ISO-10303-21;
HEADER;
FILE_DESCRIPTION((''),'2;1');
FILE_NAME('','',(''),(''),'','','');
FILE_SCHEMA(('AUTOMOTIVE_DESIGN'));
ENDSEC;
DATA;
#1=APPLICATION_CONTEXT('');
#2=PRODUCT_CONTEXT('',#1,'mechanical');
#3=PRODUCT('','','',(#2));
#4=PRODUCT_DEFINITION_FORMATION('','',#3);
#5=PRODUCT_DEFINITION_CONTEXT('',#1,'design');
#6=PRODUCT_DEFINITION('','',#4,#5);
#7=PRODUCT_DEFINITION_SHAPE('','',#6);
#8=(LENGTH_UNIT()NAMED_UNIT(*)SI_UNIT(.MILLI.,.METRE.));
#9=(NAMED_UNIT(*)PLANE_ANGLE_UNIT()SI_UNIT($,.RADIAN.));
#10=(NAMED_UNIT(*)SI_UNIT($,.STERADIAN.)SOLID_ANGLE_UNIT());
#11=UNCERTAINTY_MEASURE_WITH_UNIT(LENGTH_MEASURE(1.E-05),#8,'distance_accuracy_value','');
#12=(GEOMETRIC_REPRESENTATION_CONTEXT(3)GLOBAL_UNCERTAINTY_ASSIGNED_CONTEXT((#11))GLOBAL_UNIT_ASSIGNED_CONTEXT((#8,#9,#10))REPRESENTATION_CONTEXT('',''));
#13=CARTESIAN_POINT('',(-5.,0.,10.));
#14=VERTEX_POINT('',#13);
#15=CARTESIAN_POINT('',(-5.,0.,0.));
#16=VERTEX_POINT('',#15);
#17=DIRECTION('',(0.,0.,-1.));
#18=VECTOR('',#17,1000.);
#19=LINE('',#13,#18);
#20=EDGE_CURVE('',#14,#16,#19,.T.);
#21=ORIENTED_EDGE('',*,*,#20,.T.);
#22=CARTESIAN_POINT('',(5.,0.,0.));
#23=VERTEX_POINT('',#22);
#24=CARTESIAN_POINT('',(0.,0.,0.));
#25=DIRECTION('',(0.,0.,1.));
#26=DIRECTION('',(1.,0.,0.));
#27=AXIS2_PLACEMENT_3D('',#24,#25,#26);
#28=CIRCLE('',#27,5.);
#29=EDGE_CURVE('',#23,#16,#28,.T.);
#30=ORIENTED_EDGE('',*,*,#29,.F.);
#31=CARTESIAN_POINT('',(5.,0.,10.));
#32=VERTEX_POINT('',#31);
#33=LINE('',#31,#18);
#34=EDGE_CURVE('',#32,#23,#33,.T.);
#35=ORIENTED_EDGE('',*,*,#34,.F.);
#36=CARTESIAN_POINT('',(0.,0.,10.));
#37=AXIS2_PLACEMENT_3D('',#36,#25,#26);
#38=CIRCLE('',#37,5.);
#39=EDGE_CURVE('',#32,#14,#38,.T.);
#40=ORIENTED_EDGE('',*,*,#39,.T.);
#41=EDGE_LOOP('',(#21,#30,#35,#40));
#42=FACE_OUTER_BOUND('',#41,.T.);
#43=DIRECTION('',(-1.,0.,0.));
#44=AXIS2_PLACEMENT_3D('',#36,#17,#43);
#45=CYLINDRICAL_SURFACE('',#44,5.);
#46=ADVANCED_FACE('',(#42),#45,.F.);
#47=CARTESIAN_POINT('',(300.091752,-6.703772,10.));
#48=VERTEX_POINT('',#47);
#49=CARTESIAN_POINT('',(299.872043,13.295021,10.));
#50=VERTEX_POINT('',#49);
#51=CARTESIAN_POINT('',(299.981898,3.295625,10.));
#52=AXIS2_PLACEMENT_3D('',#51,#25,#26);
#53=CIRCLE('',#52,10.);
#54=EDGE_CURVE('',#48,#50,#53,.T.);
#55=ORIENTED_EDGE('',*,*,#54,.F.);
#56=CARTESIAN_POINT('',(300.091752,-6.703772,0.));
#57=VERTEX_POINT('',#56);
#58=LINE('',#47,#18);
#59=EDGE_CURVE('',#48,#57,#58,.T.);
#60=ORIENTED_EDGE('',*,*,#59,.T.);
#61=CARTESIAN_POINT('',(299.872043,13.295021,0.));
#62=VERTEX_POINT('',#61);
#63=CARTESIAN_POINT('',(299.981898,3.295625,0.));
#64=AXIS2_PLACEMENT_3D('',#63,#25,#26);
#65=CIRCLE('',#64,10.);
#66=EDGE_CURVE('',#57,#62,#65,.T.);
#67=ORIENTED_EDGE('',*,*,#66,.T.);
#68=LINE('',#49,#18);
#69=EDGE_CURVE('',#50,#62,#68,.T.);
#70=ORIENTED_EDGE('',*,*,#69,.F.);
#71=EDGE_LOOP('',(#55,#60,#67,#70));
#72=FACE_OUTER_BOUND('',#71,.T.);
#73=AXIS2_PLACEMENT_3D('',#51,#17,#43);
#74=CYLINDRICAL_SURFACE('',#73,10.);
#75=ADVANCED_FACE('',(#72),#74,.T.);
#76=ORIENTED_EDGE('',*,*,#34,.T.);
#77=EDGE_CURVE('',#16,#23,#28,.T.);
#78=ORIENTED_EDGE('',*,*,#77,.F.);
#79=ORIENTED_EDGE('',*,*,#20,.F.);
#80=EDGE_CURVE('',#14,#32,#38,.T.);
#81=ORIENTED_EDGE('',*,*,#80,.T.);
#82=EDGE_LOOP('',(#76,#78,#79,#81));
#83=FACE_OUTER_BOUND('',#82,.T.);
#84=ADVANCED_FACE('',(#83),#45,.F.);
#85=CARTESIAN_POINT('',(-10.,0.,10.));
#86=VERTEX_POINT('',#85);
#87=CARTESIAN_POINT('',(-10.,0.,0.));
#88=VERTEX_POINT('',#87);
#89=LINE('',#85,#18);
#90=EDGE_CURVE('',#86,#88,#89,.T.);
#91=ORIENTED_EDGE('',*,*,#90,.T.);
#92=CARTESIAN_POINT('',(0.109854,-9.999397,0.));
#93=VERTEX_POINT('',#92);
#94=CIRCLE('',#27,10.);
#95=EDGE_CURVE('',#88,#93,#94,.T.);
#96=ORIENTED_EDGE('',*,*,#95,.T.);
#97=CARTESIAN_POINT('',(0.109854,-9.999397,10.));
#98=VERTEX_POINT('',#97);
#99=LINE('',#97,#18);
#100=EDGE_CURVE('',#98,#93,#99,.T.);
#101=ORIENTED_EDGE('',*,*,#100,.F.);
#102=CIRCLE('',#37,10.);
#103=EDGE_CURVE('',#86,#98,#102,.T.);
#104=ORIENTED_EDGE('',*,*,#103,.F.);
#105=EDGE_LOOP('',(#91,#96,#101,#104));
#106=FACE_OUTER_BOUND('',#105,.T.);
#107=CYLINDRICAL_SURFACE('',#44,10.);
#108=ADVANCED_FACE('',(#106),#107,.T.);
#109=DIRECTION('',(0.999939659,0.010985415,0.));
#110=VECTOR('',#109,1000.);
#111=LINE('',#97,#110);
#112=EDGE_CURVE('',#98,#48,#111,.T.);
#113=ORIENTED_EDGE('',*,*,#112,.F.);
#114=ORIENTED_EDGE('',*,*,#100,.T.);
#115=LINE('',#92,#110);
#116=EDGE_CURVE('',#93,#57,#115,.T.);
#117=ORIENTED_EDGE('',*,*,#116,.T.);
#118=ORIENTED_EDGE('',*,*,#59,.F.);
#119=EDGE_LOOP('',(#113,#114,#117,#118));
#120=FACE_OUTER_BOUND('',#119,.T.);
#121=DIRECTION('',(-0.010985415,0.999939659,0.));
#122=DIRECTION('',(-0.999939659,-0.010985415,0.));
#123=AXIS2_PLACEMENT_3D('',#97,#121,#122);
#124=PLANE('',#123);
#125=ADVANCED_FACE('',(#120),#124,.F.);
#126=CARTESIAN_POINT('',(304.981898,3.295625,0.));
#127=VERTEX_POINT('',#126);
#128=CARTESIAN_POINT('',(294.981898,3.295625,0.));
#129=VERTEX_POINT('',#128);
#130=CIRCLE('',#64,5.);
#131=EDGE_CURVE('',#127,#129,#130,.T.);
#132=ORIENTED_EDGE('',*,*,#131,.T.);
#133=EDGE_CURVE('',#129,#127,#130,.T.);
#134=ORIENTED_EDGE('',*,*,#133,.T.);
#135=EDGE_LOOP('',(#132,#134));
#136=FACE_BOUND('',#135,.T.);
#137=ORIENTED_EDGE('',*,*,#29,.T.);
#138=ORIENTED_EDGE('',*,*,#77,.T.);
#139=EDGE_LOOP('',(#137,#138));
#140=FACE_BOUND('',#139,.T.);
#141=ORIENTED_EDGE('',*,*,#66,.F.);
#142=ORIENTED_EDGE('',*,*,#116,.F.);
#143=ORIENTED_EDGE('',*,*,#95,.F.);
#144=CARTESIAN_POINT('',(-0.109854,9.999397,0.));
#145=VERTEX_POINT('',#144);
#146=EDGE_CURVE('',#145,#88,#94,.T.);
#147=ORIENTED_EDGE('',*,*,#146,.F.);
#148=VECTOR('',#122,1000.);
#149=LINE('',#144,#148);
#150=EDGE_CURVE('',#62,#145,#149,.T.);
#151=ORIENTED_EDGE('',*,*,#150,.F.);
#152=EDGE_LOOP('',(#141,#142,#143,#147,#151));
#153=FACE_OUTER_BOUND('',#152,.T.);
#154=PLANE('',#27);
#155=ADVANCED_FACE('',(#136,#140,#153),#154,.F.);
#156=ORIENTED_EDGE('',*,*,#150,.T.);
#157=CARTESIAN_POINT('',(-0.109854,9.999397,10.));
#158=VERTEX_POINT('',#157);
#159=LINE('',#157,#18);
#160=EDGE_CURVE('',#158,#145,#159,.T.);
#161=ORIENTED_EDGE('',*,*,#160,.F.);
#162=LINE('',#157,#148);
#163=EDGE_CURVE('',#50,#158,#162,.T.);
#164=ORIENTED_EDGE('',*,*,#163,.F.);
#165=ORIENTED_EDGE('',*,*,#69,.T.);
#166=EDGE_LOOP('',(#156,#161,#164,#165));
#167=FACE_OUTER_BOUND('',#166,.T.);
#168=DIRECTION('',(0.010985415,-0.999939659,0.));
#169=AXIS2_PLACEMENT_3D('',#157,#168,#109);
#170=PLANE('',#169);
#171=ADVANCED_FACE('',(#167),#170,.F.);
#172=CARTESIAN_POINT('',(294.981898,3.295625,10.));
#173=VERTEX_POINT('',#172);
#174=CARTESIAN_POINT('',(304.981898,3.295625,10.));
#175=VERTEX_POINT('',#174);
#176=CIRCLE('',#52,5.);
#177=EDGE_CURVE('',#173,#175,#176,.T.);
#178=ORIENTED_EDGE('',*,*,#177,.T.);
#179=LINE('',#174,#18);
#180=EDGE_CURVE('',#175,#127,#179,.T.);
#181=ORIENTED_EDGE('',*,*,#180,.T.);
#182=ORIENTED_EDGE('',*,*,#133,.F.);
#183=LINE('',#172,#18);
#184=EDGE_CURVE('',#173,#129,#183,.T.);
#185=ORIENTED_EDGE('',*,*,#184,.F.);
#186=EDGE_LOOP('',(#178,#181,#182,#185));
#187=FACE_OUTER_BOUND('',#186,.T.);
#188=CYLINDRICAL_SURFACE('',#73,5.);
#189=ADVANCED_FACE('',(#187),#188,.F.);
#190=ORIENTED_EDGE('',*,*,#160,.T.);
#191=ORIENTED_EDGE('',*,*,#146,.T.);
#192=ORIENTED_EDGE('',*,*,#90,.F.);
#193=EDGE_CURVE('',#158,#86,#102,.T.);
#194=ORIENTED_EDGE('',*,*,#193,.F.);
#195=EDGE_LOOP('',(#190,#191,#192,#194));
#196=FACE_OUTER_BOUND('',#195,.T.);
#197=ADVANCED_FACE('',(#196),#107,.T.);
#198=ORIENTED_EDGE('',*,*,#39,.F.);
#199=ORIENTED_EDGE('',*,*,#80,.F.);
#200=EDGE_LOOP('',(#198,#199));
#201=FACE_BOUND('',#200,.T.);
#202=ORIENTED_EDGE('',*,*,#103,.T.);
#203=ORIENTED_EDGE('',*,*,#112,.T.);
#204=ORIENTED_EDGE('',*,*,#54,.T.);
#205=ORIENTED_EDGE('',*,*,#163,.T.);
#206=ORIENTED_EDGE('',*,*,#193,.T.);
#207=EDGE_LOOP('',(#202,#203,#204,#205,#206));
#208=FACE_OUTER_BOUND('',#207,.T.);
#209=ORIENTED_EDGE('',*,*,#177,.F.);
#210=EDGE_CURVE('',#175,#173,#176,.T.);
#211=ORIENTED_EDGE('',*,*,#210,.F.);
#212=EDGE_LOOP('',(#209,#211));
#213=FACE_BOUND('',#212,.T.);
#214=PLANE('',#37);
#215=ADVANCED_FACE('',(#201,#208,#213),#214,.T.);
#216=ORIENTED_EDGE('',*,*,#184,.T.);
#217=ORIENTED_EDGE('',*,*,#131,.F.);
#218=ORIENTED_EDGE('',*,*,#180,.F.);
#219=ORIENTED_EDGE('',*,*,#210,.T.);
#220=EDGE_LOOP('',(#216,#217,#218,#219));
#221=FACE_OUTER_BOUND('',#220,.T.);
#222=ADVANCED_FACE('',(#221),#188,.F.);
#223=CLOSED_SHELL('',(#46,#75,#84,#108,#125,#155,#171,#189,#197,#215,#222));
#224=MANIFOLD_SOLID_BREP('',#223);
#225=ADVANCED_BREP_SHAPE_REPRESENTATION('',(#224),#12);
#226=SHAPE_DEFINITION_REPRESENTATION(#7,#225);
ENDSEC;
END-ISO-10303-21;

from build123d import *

# Parameters (mm, degrees)
SKETCH1_R           = 5
BOSS_EXTRUDE1_DEPTH = 10


with BuildPart() as part:
    # Sketch1 → Boss-Extrude1 (new body)
    with BuildSketch(Plane.XY):
        with BuildLine():
            Line((-0.109854152, 9.999396585), (299.8720434, 13.295021139))
            ThreePointArc((299.8720434, 13.295021139), (309.981294137, 3.405478706), (300.091751704, -6.703772031))
            Line((300.091751704, -6.703772031), (0.109854152, -9.999396585))
            ThreePointArc((0.109854152, -9.999396585), (-9.999396585, -0.109854152), (-0.109854152, 9.999396585))
        make_face()
        with Locations((299.981897552, 3.295624554)):
            Circle(SKETCH1_R, mode=Mode.SUBTRACT)
        Circle(SKETCH1_R, mode=Mode.SUBTRACT)
    extrude(amount=BOSS_EXTRUDE1_DEPTH)


solid = part.part
